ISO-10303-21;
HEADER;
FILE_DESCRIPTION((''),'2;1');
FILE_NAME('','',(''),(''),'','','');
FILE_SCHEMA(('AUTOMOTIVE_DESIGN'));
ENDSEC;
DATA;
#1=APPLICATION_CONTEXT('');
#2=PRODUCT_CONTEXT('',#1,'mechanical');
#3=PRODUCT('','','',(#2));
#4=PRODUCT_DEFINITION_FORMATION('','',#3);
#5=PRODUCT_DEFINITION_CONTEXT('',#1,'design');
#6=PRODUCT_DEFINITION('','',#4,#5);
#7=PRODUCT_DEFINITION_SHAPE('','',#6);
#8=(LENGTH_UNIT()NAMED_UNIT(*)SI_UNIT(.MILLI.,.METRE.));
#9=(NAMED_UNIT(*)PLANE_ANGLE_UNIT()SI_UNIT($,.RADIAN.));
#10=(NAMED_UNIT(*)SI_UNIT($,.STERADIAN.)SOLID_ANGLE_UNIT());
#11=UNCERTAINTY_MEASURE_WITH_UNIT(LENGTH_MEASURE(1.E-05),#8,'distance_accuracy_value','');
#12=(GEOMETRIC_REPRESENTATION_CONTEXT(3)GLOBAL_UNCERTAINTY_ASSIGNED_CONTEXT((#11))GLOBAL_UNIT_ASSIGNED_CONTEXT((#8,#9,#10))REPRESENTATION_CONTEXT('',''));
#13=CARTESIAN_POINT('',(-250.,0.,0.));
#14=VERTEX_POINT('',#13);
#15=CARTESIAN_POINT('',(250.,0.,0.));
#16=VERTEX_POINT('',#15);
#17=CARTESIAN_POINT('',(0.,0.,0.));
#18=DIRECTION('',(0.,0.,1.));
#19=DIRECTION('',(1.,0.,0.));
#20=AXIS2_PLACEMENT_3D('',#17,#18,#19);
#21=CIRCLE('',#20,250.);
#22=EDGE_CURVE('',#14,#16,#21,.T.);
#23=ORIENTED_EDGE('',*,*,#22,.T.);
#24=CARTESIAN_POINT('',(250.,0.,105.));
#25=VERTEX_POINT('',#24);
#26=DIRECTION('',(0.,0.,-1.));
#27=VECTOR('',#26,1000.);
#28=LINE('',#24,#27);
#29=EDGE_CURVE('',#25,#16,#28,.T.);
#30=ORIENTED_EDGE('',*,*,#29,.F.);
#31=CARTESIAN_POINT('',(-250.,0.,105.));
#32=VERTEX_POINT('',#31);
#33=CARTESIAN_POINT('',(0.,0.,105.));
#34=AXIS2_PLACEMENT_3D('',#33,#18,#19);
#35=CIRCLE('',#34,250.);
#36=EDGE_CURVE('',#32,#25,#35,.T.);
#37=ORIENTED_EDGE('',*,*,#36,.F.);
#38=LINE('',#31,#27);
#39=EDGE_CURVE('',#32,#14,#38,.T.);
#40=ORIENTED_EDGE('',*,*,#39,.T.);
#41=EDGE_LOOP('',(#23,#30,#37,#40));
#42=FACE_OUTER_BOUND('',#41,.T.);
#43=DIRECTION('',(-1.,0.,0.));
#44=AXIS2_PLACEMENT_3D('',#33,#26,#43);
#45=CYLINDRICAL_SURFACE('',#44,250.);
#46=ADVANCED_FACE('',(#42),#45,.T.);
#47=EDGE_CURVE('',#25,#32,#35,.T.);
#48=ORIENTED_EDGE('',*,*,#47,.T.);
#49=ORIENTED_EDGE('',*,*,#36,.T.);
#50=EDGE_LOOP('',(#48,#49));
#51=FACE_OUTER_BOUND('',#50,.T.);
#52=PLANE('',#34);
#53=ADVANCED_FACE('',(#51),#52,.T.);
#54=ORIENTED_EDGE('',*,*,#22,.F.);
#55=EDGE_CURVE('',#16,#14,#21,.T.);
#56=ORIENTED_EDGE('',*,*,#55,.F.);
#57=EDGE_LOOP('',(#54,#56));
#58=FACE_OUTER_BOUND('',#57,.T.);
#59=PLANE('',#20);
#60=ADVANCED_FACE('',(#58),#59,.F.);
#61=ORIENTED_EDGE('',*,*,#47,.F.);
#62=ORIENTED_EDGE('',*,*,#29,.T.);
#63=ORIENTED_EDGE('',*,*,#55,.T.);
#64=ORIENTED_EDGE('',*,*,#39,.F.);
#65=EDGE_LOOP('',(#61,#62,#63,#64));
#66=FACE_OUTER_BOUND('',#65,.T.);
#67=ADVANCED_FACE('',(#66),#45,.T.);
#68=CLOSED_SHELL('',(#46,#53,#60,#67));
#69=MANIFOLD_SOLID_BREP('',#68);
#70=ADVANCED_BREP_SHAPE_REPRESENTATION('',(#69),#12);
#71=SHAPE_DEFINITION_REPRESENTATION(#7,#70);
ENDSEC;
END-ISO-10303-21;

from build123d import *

# Parameters (mm, degrees)
SKETCH1_R           = 250
BOSS_EXTRUDE1_DEPTH = 105


with BuildPart() as part:
    # Sketch1 → Boss-Extrude1 (new body)
    with BuildSketch(Plane.XY):
        Circle(SKETCH1_R)
    extrude(amount=BOSS_EXTRUDE1_DEPTH)


solid = part.part
